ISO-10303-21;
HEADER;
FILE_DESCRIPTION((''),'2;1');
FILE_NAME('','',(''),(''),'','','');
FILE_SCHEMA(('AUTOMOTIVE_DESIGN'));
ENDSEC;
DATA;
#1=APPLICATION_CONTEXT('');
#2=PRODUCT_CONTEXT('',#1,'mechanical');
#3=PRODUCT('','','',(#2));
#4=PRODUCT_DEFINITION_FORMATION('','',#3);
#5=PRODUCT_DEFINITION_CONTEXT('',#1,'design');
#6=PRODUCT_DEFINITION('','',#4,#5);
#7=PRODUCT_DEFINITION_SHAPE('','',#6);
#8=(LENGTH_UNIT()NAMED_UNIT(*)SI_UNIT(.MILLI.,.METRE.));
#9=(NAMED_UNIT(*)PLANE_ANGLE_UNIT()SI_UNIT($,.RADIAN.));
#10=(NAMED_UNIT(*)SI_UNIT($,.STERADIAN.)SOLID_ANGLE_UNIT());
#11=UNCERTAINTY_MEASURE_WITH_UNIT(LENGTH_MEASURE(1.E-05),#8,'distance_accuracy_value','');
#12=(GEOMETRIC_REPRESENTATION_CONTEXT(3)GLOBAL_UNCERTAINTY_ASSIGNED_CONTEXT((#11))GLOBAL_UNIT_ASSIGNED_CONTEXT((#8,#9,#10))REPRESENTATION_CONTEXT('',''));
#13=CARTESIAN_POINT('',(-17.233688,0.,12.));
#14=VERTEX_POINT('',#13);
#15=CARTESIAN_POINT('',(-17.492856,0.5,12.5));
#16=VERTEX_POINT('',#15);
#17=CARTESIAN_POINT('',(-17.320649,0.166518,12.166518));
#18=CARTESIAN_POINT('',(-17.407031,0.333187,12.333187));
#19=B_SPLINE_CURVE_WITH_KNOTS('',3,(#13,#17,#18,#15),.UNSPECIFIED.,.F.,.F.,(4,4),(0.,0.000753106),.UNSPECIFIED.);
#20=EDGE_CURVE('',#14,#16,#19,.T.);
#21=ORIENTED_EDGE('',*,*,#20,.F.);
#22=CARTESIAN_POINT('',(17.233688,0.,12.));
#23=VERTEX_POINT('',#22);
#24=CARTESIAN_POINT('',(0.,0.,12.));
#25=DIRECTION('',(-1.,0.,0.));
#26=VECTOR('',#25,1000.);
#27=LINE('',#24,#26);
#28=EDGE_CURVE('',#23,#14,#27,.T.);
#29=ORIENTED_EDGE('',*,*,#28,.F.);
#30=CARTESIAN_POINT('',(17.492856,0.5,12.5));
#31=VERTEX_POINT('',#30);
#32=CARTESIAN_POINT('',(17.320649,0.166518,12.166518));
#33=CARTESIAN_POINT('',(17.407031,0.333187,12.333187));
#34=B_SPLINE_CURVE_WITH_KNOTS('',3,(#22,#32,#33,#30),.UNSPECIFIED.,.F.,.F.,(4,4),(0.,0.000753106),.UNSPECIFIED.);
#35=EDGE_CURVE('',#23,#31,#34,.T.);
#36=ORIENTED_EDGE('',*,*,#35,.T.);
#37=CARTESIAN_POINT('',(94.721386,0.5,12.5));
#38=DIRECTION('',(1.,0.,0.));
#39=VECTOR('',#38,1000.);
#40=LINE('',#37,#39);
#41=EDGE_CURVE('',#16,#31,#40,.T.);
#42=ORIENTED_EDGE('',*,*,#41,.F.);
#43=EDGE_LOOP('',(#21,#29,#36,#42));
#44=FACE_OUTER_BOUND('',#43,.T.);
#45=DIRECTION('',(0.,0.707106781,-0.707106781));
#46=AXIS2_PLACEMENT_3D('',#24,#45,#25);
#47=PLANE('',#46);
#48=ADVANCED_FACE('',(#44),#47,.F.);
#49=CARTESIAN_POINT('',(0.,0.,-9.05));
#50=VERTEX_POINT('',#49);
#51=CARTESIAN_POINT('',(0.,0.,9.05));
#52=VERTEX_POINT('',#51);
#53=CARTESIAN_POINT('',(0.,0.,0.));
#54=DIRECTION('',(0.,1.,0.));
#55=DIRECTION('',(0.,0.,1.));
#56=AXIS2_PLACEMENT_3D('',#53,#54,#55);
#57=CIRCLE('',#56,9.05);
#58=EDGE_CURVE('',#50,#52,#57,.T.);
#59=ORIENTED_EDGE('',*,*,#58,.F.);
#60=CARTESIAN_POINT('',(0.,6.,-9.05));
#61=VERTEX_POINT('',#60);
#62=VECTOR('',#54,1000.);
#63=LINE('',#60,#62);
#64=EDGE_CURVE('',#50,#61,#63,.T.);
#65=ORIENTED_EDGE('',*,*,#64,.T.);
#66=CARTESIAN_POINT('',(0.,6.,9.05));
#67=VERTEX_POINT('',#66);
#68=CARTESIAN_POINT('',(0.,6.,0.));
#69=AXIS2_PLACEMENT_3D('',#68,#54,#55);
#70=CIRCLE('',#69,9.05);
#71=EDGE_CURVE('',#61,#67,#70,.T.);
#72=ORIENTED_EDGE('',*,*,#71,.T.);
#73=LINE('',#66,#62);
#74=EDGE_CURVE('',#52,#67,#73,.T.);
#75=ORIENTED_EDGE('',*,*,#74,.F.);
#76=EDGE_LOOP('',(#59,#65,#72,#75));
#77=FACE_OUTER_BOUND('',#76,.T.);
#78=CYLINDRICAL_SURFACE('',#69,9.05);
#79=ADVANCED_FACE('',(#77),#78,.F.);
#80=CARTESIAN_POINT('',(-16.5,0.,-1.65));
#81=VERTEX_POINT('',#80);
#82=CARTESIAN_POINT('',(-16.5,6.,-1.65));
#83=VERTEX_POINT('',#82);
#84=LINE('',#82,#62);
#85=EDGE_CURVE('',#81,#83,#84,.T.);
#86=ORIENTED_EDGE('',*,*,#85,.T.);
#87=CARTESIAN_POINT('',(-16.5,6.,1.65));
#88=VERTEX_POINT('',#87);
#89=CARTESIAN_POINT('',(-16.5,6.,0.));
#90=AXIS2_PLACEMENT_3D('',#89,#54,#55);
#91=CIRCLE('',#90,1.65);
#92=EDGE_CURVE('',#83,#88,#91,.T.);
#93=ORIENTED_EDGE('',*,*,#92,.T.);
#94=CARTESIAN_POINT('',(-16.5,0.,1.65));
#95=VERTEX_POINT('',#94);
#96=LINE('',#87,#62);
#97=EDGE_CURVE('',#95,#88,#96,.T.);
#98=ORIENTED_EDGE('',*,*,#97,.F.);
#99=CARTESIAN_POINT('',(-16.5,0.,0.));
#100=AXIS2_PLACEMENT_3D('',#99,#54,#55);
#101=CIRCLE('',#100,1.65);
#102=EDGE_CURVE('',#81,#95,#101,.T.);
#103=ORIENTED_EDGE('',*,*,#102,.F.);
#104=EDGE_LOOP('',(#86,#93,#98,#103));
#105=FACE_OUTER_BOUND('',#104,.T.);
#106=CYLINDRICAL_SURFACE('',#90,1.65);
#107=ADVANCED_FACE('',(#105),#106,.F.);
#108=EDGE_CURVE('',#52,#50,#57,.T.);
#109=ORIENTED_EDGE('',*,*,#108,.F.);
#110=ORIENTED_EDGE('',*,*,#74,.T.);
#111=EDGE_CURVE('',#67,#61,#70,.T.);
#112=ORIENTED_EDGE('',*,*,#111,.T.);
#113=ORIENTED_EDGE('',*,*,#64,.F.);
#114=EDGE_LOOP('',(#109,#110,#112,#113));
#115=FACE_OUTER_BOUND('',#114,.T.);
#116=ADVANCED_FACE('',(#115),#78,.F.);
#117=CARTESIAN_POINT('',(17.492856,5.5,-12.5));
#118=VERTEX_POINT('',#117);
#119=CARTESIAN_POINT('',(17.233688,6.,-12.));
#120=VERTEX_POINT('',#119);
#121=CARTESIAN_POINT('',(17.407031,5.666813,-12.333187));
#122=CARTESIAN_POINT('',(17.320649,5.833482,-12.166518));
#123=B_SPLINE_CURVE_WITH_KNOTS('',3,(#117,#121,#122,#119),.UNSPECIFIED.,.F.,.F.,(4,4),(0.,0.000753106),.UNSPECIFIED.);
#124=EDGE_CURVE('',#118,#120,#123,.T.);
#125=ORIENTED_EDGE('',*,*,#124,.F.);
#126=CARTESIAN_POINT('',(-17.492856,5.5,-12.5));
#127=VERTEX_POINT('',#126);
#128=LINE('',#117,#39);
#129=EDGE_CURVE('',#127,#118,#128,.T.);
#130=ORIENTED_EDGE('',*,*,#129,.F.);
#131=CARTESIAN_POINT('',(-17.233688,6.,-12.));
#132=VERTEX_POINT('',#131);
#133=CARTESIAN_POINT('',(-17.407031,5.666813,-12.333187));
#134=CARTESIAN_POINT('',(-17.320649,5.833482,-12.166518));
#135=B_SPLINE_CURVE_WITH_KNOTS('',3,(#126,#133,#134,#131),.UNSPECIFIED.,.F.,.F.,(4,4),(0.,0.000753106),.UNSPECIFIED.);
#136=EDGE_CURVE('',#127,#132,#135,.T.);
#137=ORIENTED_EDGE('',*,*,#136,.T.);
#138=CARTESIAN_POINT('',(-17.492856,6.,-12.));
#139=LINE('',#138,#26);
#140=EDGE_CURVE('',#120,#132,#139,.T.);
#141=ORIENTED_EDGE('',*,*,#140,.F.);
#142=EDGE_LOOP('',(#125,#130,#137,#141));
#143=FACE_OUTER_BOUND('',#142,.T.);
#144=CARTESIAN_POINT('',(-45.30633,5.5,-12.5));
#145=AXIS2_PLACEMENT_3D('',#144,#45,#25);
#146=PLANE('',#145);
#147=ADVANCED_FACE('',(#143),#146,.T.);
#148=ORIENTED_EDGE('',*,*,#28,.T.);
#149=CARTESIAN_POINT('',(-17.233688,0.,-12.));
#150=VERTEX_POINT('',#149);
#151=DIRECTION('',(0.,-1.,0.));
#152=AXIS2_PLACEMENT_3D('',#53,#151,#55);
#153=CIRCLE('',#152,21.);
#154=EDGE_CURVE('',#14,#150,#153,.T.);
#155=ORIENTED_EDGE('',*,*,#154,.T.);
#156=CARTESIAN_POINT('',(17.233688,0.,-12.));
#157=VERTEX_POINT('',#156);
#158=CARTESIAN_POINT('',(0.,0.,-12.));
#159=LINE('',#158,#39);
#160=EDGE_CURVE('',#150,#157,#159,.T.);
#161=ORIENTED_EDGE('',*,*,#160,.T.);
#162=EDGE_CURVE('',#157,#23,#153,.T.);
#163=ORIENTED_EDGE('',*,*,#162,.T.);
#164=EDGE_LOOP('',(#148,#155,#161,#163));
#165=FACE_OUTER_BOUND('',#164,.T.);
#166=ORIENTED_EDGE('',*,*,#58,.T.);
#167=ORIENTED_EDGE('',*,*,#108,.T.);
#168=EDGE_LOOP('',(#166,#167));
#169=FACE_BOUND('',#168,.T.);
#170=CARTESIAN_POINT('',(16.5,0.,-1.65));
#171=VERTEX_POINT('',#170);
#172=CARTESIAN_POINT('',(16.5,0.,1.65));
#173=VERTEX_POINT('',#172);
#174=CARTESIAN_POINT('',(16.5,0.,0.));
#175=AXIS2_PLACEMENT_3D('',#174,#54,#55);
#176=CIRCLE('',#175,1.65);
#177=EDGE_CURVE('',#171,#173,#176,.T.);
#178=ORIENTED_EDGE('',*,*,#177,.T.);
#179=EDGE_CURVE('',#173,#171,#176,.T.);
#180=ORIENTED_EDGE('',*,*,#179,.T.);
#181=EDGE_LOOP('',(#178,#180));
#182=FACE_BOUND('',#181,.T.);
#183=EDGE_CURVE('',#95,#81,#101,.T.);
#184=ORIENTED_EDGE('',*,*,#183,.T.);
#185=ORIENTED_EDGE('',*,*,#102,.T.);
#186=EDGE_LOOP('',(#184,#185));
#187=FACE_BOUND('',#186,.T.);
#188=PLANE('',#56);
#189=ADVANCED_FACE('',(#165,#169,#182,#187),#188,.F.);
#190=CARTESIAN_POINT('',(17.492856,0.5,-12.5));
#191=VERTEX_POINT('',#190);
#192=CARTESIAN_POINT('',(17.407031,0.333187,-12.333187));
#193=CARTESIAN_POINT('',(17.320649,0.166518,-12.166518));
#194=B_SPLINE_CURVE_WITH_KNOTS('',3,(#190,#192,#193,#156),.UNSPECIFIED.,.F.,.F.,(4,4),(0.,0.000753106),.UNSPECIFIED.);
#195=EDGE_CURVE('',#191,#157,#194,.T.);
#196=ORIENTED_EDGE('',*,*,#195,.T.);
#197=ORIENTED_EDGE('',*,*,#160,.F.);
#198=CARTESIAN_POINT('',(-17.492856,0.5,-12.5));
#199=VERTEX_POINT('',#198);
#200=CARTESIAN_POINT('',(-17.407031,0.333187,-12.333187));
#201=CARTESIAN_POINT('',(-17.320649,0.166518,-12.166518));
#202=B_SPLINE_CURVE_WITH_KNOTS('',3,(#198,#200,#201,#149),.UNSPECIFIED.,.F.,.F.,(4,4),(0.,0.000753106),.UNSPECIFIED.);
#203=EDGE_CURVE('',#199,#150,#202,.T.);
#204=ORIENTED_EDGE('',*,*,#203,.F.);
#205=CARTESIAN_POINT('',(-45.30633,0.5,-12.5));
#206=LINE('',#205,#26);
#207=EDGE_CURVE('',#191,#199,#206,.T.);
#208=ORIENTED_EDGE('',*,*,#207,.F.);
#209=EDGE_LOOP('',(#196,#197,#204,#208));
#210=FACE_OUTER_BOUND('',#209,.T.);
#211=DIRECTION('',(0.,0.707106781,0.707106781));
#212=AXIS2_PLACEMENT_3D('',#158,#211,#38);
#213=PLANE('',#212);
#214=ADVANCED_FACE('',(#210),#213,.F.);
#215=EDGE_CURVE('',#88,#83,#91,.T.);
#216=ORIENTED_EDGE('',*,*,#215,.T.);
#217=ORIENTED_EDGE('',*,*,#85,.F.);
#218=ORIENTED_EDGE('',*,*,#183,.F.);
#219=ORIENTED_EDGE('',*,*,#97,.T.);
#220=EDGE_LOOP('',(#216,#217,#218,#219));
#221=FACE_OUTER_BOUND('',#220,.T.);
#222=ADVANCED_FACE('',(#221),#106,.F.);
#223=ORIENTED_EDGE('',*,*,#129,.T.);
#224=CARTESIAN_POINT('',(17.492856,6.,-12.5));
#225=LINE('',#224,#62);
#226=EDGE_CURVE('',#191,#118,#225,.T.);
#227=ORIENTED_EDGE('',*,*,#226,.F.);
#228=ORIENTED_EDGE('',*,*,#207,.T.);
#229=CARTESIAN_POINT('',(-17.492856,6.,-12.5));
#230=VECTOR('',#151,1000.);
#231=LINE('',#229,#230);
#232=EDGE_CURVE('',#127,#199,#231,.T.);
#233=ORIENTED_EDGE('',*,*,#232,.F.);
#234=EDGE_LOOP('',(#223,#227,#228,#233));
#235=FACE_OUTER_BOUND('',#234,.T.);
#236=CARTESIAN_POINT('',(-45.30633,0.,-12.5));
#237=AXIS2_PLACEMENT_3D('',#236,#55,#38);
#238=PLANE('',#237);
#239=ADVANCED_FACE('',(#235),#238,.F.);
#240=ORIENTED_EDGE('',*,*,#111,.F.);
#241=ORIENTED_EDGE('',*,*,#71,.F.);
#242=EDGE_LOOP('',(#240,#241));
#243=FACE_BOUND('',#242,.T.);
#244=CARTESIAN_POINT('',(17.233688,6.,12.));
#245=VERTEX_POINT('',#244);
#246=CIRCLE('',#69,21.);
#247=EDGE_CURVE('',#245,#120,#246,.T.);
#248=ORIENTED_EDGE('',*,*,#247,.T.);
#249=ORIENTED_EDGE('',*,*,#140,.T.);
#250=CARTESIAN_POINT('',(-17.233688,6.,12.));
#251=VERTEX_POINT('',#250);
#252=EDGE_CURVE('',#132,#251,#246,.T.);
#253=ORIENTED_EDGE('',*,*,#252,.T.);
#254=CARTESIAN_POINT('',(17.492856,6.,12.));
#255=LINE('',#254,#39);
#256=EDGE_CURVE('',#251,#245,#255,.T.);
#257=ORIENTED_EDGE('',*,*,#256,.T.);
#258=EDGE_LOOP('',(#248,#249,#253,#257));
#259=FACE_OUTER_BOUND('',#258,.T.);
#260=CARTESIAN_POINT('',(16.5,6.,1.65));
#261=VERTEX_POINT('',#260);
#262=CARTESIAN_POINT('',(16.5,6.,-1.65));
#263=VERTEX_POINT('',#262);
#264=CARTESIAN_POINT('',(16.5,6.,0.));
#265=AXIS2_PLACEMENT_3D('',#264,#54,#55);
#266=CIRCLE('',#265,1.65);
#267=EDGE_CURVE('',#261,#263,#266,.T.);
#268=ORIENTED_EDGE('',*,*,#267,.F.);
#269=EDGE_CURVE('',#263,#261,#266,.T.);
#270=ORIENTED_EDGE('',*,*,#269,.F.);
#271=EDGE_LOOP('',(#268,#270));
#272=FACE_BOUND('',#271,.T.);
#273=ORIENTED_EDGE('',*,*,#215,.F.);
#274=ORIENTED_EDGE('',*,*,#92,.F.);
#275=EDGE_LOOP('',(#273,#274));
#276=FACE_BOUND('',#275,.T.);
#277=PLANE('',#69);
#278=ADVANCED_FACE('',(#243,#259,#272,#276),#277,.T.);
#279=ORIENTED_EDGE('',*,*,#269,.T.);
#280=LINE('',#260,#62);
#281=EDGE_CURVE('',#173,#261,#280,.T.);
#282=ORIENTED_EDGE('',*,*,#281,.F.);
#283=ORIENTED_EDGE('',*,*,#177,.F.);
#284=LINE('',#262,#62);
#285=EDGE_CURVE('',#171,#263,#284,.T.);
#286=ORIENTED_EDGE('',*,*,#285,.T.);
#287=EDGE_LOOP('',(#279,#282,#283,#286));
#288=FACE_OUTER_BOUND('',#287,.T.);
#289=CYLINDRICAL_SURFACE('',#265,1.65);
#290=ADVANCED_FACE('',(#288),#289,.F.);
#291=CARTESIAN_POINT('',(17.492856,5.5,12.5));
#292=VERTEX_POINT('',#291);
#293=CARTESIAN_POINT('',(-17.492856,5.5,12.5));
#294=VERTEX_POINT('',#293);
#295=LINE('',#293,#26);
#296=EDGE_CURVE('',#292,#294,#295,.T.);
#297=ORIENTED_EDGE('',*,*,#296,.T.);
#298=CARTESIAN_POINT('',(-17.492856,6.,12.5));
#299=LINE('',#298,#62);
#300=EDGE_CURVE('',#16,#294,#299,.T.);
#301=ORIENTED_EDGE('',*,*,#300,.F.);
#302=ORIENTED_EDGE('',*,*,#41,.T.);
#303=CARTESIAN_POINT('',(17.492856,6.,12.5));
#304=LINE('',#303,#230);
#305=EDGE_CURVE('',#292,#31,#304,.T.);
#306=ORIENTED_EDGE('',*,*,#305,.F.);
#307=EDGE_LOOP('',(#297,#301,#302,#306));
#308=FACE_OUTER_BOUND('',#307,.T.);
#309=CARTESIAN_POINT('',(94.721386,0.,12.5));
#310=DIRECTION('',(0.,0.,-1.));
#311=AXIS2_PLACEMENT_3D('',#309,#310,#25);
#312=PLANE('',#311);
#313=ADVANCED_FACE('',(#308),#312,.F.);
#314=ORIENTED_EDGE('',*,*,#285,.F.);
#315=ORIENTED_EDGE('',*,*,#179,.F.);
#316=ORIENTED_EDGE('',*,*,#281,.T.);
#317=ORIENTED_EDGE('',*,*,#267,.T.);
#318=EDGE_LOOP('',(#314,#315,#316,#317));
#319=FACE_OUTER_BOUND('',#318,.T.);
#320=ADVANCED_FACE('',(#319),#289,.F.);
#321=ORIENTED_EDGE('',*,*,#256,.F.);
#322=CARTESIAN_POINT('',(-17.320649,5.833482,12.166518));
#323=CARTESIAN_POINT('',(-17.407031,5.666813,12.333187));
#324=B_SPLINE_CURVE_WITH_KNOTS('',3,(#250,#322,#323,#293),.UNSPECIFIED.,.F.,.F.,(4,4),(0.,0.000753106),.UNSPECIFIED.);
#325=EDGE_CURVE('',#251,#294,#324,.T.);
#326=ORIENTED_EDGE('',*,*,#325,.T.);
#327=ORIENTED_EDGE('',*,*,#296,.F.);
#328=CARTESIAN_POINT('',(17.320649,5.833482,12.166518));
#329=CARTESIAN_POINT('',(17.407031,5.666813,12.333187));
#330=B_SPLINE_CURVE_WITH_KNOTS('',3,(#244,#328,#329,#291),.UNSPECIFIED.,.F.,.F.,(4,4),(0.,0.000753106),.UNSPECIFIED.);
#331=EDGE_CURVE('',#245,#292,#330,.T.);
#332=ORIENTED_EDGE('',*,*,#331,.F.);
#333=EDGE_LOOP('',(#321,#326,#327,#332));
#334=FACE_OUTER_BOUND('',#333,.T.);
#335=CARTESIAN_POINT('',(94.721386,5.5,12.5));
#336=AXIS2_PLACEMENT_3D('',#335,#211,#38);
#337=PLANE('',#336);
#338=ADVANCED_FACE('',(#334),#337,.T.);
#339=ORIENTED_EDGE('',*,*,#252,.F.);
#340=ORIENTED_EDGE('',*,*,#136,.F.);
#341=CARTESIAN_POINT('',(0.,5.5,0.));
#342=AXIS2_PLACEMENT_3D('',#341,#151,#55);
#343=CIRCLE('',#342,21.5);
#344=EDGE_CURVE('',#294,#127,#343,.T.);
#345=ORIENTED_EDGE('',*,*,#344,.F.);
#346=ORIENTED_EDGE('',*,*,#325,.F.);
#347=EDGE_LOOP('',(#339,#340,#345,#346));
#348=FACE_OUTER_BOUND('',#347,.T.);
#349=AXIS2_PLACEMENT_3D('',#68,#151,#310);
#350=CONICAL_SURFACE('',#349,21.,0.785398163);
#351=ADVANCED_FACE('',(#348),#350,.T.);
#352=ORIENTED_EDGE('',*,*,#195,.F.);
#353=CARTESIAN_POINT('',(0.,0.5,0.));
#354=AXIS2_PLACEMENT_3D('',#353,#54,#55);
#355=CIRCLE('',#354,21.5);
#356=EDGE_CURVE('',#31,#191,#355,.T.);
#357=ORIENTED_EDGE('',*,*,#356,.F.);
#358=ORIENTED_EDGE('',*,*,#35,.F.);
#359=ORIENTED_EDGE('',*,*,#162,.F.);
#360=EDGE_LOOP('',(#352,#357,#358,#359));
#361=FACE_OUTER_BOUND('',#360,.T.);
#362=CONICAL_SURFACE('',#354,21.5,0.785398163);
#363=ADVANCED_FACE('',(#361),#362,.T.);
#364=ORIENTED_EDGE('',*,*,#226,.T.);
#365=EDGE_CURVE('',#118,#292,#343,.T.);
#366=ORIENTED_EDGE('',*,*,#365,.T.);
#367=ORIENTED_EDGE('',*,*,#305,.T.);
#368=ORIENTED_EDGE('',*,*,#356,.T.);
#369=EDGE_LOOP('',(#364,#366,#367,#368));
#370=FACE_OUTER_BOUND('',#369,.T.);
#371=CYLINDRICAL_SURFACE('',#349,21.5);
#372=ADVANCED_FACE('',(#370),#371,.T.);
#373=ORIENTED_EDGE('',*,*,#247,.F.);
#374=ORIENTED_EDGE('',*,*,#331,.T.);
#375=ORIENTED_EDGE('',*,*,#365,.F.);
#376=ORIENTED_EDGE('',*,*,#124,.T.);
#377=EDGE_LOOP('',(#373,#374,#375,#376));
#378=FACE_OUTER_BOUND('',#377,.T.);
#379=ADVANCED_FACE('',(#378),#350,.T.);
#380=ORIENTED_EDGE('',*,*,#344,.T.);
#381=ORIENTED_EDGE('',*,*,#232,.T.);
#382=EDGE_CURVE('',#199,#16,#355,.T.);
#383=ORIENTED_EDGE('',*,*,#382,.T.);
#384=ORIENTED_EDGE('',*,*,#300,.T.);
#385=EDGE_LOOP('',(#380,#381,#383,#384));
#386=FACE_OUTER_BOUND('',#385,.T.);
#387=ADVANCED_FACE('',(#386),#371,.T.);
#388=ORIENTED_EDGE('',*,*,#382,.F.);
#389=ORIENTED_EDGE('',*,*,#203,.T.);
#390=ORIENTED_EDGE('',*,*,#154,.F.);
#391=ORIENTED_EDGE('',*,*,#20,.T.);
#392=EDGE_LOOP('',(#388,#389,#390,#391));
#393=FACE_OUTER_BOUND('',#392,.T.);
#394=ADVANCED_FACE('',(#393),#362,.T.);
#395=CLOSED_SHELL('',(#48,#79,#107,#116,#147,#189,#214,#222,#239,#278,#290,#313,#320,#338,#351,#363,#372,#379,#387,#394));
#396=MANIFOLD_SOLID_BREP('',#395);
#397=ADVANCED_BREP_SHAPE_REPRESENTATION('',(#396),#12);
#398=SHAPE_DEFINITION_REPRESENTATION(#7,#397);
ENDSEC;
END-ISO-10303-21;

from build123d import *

# Parameters (mm, degrees)
SKETCH_1_R          = 21.5
EXTRUDE_1_DEPTH     = 6
HOLE_WIZARD_M4_1_D  = 3.3
SKETCH_5_W          = 80.188195039
SKETCH_5_H          = 23.165478567
SKETCH_5_W_2        = 146.4427716
SKETCH_5_H_2        = 26.907594335
CUT_EXTRUDE_1_DEPTH = 31.991934435
HOLE_WIZARD_M20_2_D = 18.1
CHAMFER_1_SIZE      = 0.5


with BuildPart() as part:
    # 草图1 → 凸台-拉伸1 (new body)
    with BuildSketch(Plane(origin=(0, 0, 0), x_dir=(1, 0, 0), z_dir=(0, 1, 0))):
        with Locations(Location((0, 0, 0), (0, 0, 270))):
            Circle(SKETCH_1_R)
    extrude(amount=EXTRUDE_1_DEPTH)

    # M4 螺纹孔1 (through all)
    with Locations(Plane(origin=(0, 6, 0), x_dir=(1, 0, 0), z_dir=(0, 1, 0))):
        with Locations((-16.5, 0), (16.5, 0)):
            Hole(HOLE_WIZARD_M4_1_D / 2)

    # 草图5 → 切除-拉伸1 (cut, through all)
    with BuildSketch(Plane(origin=(0, 6, 0), x_dir=(1, 0, 0), z_dir=(0, 1, 0))):
        with Locations((-5.212232678, 24.082739284)):
            Rectangle(SKETCH_5_W, SKETCH_5_H)
        with Locations((21.5, -25.953797168)):
            Rectangle(SKETCH_5_W_2, SKETCH_5_H_2)
    extrude(amount=-CUT_EXTRUDE_1_DEPTH, mode=Mode.SUBTRACT)

    # M20 螺纹孔2 (through all)
    with Locations(Plane(origin=(0, 6, 0), x_dir=(1, 0, 0), z_dir=(0, 1, 0))):
        with Locations((0, 0)):
            Hole(HOLE_WIZARD_M20_2_D / 2)

    # 倒角1
    chamfer_1_edges = [part.edges().sort_by_distance(p)[0] for p in [
        (-21.5, 0, 0),
        (0, 0, -12.5),
        (-21.5, 6, 0),
        (0, 6, -12.5),
        (21.5, 0, 0),
        (0, 0, 12.5),
        (21.5, 6, 0),
        (0, 6, 12.5),
    ]]
    chamfer(chamfer_1_edges, length=CHAMFER_1_SIZE)


solid = part.part
